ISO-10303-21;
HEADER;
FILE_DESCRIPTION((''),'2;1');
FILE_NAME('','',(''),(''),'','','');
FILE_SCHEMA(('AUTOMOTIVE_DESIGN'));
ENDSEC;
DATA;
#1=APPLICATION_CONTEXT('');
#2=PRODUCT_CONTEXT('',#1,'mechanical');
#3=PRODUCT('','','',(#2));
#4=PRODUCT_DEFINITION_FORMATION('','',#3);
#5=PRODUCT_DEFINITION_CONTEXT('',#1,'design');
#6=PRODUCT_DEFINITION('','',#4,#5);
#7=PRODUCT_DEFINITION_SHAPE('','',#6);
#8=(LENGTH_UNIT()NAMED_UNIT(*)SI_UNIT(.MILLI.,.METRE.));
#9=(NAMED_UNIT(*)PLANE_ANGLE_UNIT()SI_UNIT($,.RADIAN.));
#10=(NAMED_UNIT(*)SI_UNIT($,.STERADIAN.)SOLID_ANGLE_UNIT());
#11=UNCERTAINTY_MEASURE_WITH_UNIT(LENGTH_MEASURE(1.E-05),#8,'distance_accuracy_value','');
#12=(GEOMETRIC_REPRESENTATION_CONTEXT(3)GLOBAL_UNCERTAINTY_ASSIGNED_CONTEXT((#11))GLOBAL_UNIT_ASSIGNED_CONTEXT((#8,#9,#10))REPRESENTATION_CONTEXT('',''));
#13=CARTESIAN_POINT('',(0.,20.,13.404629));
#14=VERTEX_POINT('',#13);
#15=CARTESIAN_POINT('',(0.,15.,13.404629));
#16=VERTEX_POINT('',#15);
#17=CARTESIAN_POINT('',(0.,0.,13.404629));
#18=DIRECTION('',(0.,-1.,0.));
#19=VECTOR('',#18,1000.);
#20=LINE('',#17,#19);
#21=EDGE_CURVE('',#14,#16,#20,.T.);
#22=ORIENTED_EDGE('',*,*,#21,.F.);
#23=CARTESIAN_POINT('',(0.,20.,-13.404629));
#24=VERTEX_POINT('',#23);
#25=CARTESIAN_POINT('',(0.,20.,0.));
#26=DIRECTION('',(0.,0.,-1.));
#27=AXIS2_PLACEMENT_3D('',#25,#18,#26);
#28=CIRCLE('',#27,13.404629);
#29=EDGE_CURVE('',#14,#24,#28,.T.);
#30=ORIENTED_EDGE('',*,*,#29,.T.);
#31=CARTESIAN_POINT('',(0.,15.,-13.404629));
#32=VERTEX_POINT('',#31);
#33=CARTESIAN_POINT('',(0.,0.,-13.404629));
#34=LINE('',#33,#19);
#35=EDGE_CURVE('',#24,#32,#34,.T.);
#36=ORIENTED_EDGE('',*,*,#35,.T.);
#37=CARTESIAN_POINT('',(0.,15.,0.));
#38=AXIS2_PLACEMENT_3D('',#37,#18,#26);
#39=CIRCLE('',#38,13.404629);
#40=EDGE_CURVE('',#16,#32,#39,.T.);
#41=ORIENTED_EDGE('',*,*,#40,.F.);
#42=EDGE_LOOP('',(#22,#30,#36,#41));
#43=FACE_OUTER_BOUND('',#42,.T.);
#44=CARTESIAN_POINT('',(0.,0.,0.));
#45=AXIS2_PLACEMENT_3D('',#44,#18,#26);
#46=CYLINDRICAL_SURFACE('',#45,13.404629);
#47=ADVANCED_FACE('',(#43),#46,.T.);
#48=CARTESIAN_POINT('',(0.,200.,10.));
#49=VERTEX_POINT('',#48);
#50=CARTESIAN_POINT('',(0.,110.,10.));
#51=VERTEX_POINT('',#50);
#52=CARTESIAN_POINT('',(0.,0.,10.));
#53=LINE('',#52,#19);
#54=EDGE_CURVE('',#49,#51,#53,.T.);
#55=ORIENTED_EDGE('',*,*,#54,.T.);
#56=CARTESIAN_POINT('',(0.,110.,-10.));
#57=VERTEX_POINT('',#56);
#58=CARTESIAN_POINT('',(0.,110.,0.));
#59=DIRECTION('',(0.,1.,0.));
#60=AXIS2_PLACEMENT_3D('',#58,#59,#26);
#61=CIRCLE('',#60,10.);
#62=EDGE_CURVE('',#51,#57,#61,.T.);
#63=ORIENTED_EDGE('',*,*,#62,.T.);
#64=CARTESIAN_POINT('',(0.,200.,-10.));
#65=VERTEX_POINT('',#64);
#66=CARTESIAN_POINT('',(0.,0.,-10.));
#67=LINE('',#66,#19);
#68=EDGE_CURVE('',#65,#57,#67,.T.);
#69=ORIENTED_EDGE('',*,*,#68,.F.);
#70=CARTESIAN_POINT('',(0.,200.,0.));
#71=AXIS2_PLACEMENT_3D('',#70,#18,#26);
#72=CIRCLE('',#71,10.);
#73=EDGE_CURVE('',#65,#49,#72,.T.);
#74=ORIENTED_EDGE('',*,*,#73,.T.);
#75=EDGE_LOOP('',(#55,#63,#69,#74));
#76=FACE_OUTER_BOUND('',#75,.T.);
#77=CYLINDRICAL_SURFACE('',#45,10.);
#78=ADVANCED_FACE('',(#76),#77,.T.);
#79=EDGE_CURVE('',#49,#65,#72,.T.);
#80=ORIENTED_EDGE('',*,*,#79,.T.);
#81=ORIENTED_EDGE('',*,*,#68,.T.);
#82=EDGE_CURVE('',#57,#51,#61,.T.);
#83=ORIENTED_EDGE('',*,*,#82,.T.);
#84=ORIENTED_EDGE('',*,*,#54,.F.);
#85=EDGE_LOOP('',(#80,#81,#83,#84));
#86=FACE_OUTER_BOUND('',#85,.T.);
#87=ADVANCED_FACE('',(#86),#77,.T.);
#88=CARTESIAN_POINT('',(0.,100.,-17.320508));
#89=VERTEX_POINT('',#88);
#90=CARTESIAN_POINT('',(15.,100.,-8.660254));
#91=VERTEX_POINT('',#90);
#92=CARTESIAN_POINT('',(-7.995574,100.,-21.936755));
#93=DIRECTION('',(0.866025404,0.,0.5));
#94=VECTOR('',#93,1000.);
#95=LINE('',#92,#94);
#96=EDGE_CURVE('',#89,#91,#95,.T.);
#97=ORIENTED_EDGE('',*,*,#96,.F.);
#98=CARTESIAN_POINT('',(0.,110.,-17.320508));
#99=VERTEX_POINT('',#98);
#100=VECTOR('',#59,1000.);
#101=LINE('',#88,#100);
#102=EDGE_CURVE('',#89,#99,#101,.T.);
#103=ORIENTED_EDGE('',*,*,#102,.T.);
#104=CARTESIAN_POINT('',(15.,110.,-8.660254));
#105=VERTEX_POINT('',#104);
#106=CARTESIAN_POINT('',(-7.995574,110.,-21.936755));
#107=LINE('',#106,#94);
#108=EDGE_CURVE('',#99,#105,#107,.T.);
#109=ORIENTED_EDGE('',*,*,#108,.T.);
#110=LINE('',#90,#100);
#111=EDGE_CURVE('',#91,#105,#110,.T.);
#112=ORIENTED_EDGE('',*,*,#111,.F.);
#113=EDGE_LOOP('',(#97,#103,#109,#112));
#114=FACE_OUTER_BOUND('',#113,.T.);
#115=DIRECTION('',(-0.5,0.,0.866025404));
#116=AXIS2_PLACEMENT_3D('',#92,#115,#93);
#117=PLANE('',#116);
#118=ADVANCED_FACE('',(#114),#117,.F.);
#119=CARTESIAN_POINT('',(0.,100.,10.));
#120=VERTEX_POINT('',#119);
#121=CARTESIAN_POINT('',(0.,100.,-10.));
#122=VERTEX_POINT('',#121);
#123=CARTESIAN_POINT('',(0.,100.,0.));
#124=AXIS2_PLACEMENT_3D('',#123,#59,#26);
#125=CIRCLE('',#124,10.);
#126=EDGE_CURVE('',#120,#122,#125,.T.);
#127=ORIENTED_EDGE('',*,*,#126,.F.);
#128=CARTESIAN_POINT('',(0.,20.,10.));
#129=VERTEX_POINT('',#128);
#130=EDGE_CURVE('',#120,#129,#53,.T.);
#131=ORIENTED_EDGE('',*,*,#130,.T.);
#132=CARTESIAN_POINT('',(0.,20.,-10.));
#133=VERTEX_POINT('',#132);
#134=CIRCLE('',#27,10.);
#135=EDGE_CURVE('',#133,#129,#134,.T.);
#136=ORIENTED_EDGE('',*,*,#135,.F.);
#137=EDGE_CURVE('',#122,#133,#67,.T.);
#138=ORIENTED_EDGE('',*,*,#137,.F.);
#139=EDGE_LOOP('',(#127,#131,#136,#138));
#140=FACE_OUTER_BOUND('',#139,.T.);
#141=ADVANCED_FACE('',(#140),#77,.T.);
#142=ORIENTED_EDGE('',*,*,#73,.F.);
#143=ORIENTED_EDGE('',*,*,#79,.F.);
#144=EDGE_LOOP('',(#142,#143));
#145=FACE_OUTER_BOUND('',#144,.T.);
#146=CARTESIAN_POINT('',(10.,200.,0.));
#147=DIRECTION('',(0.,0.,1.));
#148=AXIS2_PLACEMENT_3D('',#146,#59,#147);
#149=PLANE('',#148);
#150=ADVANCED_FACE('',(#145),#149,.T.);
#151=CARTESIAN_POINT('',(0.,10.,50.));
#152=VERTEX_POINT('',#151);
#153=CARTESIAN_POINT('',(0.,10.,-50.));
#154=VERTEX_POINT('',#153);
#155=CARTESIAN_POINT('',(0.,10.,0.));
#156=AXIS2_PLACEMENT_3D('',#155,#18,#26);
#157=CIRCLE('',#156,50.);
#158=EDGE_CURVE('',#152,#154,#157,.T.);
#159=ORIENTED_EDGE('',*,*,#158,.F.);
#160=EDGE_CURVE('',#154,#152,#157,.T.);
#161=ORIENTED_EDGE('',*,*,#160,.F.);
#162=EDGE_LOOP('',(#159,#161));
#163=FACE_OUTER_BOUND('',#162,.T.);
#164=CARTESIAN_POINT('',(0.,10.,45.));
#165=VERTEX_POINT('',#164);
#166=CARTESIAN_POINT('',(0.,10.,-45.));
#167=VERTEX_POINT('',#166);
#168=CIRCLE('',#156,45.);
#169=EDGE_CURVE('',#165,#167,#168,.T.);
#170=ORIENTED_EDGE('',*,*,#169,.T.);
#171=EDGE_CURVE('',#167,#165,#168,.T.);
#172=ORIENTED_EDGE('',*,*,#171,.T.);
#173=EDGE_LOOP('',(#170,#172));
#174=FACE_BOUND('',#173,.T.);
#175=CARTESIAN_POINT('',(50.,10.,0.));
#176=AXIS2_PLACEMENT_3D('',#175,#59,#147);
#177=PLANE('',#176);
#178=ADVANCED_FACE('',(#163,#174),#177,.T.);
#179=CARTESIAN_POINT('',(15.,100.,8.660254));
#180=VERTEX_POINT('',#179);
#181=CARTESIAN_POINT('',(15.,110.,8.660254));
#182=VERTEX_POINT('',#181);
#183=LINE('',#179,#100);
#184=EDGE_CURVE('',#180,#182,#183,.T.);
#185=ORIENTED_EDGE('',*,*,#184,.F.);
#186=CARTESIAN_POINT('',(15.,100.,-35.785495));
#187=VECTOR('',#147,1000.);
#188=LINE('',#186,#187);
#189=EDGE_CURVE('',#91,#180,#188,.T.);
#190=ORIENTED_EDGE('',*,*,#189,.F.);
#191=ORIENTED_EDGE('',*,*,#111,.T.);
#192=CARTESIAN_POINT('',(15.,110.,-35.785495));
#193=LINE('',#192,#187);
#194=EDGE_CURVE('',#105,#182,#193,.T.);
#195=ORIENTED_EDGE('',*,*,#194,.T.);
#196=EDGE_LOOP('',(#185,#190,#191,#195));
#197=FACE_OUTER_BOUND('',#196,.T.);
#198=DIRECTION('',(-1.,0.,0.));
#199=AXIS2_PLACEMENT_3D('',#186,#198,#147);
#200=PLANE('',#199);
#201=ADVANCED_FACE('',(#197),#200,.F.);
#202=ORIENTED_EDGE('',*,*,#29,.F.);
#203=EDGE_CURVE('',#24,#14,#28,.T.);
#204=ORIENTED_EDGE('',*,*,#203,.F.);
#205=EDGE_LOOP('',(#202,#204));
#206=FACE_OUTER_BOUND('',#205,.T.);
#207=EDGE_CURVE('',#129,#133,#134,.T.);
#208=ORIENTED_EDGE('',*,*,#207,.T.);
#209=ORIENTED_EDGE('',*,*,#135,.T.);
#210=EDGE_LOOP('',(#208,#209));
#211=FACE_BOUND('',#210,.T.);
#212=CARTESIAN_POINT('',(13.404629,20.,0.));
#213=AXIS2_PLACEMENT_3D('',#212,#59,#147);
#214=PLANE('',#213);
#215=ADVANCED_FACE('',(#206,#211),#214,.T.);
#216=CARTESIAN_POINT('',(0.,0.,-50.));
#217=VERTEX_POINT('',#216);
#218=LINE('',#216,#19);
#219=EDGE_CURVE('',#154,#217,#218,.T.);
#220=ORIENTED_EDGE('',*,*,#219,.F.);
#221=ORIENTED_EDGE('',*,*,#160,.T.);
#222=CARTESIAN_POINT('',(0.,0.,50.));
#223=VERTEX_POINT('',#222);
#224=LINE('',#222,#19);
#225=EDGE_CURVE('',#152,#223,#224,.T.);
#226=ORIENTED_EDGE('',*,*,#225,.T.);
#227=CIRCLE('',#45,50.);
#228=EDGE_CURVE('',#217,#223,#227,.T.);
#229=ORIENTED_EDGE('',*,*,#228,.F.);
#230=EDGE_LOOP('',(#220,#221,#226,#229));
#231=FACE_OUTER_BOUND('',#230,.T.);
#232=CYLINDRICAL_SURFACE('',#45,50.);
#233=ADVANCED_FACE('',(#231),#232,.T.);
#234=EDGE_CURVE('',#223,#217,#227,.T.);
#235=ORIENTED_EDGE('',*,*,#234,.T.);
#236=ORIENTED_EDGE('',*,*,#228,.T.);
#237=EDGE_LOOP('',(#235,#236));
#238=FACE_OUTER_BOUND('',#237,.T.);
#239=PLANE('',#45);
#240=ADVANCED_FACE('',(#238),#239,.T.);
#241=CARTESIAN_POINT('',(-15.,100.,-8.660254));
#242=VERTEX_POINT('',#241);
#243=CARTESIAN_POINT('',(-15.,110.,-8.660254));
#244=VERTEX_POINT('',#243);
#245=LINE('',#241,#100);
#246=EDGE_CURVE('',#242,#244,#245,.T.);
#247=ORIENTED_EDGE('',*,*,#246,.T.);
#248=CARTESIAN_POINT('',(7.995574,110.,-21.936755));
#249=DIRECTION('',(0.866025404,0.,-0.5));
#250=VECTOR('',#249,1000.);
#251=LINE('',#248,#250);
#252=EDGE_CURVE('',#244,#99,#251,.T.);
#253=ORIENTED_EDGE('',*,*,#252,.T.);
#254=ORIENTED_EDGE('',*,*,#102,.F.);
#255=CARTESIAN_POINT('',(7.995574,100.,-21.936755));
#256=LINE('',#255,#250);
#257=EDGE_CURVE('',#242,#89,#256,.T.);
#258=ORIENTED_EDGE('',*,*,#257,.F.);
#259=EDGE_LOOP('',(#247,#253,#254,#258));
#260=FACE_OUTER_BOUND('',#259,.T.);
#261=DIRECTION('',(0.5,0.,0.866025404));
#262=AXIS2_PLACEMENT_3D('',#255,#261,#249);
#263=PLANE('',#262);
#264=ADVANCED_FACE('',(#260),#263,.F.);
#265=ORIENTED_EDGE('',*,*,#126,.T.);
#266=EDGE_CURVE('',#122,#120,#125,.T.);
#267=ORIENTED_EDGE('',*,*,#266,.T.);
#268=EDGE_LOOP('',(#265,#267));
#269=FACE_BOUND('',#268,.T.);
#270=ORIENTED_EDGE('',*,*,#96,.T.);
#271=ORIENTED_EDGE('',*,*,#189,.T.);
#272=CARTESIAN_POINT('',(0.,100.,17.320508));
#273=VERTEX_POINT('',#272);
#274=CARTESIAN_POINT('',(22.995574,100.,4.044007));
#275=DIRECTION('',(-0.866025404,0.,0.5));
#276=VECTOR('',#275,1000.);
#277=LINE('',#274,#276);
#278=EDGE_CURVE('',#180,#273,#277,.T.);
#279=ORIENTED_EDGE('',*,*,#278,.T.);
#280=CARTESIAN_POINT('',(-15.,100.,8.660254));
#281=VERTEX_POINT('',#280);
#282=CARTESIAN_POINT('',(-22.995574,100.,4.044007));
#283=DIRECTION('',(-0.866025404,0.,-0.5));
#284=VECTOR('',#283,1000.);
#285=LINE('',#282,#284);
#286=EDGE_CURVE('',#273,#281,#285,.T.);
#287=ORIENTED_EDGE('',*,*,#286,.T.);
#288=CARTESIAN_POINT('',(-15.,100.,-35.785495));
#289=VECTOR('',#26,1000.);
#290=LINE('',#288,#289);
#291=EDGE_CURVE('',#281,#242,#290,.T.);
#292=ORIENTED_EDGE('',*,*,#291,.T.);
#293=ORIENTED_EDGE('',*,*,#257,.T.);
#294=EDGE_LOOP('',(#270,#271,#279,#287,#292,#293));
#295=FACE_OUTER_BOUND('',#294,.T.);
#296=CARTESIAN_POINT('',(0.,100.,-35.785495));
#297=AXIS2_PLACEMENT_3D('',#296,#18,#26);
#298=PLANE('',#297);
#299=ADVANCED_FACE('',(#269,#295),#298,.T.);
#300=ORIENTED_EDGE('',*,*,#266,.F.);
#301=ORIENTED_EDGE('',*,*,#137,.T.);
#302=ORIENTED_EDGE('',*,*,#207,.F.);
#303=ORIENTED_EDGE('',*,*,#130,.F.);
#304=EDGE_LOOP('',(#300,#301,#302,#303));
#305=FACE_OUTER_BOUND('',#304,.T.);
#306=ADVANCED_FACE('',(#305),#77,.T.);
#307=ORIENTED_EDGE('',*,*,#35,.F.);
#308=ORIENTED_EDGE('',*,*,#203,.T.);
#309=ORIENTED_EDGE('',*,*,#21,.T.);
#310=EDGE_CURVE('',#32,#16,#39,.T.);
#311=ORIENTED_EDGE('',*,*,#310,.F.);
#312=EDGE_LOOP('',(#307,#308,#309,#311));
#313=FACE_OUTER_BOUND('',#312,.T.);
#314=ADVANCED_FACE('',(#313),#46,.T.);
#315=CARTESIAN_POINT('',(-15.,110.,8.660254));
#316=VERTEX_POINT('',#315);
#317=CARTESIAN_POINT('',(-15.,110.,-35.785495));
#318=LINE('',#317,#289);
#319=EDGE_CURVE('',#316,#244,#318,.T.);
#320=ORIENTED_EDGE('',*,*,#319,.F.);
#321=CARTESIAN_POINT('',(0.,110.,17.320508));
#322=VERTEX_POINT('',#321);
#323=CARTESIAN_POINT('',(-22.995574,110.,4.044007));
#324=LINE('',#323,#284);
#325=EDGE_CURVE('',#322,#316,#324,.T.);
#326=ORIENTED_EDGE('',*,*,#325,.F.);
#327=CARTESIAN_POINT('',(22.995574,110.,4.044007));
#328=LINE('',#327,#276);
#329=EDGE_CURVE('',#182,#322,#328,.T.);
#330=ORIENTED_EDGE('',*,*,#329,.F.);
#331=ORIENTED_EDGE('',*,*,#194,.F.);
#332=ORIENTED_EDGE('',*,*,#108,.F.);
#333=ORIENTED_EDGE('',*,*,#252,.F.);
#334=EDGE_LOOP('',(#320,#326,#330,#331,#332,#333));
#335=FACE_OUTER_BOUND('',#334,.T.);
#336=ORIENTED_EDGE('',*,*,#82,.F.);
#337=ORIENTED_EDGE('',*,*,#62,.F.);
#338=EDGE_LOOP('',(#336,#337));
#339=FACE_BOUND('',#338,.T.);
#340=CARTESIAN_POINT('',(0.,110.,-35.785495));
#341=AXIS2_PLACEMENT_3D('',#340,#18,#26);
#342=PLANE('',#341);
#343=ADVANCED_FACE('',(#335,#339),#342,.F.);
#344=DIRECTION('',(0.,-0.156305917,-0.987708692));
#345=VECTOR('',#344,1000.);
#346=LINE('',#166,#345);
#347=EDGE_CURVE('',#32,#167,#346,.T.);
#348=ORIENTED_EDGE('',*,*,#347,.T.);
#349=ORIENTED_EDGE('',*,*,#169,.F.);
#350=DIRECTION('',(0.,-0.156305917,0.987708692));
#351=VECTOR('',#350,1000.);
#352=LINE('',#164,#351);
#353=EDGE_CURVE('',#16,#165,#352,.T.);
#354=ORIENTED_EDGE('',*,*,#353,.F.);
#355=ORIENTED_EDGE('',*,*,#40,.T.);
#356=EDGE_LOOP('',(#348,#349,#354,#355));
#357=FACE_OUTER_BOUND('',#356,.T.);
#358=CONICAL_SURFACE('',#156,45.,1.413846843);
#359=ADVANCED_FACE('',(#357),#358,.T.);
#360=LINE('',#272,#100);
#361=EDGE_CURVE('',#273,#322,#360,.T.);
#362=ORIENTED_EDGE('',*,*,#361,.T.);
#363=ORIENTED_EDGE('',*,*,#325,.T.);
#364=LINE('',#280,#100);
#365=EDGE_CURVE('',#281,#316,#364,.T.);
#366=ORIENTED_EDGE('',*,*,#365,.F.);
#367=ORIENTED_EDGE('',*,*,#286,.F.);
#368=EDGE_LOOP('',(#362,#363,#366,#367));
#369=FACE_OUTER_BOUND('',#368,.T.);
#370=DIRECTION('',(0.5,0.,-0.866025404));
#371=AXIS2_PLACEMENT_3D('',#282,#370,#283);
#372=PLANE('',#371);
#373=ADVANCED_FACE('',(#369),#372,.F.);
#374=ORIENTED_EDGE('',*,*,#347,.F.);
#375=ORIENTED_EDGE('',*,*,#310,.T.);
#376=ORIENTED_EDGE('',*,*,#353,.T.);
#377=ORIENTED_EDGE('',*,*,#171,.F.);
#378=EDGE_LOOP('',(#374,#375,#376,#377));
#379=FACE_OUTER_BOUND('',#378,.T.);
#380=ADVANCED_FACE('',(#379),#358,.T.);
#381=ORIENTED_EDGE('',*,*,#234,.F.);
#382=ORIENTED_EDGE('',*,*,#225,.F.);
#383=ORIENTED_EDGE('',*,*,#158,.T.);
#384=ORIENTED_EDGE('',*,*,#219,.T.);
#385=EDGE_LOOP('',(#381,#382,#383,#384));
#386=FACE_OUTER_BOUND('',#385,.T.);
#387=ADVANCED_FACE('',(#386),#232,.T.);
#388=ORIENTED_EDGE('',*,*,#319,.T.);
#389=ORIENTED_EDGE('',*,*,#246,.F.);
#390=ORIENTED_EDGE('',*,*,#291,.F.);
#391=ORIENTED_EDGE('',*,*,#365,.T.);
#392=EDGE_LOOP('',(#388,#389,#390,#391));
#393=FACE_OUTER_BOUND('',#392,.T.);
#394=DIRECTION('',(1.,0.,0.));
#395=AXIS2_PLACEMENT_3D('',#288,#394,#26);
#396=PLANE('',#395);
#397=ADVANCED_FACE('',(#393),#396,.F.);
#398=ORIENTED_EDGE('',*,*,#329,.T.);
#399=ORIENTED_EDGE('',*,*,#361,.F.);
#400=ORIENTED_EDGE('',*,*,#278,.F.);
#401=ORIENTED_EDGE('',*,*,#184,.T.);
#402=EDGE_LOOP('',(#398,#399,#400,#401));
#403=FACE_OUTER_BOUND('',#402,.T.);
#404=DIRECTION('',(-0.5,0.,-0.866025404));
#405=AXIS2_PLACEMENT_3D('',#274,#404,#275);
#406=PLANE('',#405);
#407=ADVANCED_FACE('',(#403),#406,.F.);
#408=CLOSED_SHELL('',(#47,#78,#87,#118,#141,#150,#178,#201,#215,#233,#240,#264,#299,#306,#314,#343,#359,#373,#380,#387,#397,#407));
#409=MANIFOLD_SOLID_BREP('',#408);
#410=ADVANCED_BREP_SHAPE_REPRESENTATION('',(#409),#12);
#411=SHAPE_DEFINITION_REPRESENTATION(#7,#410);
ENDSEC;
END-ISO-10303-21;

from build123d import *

# Parameters (mm, degrees)
EXTRUDE1_DEPTH = 10


with BuildPart() as part:
    # Sketch1 → Revolve1 (revolve)
    with BuildSketch(Plane.XY, mode=Mode.PRIVATE) as revolve1_sk:
        Polygon((0, 0), (50, 0), (50, 10), (45, 10), (13.404628949, 15), (13.404628949, 20), (10, 20), (10, 200), (0, 200), align=None)
    revolve(revolve1_sk.sketch.rotate(Axis((0, 0, 0), (0, 1, 0)), 90), axis=Axis((0, 0, 0), (0, 1, 0)))

    # Sketch2 → Extrude1 (add)
    with BuildSketch(Plane.XZ.offset(-110)):
        Polygon((0, 17.320508076), (-15, 8.660254038), (-15, -8.660254038), (0, -17.320508076), (15, -8.660254038), (15, 8.660254038), align=None)
    extrude(amount=EXTRUDE1_DEPTH)


solid = part.part
